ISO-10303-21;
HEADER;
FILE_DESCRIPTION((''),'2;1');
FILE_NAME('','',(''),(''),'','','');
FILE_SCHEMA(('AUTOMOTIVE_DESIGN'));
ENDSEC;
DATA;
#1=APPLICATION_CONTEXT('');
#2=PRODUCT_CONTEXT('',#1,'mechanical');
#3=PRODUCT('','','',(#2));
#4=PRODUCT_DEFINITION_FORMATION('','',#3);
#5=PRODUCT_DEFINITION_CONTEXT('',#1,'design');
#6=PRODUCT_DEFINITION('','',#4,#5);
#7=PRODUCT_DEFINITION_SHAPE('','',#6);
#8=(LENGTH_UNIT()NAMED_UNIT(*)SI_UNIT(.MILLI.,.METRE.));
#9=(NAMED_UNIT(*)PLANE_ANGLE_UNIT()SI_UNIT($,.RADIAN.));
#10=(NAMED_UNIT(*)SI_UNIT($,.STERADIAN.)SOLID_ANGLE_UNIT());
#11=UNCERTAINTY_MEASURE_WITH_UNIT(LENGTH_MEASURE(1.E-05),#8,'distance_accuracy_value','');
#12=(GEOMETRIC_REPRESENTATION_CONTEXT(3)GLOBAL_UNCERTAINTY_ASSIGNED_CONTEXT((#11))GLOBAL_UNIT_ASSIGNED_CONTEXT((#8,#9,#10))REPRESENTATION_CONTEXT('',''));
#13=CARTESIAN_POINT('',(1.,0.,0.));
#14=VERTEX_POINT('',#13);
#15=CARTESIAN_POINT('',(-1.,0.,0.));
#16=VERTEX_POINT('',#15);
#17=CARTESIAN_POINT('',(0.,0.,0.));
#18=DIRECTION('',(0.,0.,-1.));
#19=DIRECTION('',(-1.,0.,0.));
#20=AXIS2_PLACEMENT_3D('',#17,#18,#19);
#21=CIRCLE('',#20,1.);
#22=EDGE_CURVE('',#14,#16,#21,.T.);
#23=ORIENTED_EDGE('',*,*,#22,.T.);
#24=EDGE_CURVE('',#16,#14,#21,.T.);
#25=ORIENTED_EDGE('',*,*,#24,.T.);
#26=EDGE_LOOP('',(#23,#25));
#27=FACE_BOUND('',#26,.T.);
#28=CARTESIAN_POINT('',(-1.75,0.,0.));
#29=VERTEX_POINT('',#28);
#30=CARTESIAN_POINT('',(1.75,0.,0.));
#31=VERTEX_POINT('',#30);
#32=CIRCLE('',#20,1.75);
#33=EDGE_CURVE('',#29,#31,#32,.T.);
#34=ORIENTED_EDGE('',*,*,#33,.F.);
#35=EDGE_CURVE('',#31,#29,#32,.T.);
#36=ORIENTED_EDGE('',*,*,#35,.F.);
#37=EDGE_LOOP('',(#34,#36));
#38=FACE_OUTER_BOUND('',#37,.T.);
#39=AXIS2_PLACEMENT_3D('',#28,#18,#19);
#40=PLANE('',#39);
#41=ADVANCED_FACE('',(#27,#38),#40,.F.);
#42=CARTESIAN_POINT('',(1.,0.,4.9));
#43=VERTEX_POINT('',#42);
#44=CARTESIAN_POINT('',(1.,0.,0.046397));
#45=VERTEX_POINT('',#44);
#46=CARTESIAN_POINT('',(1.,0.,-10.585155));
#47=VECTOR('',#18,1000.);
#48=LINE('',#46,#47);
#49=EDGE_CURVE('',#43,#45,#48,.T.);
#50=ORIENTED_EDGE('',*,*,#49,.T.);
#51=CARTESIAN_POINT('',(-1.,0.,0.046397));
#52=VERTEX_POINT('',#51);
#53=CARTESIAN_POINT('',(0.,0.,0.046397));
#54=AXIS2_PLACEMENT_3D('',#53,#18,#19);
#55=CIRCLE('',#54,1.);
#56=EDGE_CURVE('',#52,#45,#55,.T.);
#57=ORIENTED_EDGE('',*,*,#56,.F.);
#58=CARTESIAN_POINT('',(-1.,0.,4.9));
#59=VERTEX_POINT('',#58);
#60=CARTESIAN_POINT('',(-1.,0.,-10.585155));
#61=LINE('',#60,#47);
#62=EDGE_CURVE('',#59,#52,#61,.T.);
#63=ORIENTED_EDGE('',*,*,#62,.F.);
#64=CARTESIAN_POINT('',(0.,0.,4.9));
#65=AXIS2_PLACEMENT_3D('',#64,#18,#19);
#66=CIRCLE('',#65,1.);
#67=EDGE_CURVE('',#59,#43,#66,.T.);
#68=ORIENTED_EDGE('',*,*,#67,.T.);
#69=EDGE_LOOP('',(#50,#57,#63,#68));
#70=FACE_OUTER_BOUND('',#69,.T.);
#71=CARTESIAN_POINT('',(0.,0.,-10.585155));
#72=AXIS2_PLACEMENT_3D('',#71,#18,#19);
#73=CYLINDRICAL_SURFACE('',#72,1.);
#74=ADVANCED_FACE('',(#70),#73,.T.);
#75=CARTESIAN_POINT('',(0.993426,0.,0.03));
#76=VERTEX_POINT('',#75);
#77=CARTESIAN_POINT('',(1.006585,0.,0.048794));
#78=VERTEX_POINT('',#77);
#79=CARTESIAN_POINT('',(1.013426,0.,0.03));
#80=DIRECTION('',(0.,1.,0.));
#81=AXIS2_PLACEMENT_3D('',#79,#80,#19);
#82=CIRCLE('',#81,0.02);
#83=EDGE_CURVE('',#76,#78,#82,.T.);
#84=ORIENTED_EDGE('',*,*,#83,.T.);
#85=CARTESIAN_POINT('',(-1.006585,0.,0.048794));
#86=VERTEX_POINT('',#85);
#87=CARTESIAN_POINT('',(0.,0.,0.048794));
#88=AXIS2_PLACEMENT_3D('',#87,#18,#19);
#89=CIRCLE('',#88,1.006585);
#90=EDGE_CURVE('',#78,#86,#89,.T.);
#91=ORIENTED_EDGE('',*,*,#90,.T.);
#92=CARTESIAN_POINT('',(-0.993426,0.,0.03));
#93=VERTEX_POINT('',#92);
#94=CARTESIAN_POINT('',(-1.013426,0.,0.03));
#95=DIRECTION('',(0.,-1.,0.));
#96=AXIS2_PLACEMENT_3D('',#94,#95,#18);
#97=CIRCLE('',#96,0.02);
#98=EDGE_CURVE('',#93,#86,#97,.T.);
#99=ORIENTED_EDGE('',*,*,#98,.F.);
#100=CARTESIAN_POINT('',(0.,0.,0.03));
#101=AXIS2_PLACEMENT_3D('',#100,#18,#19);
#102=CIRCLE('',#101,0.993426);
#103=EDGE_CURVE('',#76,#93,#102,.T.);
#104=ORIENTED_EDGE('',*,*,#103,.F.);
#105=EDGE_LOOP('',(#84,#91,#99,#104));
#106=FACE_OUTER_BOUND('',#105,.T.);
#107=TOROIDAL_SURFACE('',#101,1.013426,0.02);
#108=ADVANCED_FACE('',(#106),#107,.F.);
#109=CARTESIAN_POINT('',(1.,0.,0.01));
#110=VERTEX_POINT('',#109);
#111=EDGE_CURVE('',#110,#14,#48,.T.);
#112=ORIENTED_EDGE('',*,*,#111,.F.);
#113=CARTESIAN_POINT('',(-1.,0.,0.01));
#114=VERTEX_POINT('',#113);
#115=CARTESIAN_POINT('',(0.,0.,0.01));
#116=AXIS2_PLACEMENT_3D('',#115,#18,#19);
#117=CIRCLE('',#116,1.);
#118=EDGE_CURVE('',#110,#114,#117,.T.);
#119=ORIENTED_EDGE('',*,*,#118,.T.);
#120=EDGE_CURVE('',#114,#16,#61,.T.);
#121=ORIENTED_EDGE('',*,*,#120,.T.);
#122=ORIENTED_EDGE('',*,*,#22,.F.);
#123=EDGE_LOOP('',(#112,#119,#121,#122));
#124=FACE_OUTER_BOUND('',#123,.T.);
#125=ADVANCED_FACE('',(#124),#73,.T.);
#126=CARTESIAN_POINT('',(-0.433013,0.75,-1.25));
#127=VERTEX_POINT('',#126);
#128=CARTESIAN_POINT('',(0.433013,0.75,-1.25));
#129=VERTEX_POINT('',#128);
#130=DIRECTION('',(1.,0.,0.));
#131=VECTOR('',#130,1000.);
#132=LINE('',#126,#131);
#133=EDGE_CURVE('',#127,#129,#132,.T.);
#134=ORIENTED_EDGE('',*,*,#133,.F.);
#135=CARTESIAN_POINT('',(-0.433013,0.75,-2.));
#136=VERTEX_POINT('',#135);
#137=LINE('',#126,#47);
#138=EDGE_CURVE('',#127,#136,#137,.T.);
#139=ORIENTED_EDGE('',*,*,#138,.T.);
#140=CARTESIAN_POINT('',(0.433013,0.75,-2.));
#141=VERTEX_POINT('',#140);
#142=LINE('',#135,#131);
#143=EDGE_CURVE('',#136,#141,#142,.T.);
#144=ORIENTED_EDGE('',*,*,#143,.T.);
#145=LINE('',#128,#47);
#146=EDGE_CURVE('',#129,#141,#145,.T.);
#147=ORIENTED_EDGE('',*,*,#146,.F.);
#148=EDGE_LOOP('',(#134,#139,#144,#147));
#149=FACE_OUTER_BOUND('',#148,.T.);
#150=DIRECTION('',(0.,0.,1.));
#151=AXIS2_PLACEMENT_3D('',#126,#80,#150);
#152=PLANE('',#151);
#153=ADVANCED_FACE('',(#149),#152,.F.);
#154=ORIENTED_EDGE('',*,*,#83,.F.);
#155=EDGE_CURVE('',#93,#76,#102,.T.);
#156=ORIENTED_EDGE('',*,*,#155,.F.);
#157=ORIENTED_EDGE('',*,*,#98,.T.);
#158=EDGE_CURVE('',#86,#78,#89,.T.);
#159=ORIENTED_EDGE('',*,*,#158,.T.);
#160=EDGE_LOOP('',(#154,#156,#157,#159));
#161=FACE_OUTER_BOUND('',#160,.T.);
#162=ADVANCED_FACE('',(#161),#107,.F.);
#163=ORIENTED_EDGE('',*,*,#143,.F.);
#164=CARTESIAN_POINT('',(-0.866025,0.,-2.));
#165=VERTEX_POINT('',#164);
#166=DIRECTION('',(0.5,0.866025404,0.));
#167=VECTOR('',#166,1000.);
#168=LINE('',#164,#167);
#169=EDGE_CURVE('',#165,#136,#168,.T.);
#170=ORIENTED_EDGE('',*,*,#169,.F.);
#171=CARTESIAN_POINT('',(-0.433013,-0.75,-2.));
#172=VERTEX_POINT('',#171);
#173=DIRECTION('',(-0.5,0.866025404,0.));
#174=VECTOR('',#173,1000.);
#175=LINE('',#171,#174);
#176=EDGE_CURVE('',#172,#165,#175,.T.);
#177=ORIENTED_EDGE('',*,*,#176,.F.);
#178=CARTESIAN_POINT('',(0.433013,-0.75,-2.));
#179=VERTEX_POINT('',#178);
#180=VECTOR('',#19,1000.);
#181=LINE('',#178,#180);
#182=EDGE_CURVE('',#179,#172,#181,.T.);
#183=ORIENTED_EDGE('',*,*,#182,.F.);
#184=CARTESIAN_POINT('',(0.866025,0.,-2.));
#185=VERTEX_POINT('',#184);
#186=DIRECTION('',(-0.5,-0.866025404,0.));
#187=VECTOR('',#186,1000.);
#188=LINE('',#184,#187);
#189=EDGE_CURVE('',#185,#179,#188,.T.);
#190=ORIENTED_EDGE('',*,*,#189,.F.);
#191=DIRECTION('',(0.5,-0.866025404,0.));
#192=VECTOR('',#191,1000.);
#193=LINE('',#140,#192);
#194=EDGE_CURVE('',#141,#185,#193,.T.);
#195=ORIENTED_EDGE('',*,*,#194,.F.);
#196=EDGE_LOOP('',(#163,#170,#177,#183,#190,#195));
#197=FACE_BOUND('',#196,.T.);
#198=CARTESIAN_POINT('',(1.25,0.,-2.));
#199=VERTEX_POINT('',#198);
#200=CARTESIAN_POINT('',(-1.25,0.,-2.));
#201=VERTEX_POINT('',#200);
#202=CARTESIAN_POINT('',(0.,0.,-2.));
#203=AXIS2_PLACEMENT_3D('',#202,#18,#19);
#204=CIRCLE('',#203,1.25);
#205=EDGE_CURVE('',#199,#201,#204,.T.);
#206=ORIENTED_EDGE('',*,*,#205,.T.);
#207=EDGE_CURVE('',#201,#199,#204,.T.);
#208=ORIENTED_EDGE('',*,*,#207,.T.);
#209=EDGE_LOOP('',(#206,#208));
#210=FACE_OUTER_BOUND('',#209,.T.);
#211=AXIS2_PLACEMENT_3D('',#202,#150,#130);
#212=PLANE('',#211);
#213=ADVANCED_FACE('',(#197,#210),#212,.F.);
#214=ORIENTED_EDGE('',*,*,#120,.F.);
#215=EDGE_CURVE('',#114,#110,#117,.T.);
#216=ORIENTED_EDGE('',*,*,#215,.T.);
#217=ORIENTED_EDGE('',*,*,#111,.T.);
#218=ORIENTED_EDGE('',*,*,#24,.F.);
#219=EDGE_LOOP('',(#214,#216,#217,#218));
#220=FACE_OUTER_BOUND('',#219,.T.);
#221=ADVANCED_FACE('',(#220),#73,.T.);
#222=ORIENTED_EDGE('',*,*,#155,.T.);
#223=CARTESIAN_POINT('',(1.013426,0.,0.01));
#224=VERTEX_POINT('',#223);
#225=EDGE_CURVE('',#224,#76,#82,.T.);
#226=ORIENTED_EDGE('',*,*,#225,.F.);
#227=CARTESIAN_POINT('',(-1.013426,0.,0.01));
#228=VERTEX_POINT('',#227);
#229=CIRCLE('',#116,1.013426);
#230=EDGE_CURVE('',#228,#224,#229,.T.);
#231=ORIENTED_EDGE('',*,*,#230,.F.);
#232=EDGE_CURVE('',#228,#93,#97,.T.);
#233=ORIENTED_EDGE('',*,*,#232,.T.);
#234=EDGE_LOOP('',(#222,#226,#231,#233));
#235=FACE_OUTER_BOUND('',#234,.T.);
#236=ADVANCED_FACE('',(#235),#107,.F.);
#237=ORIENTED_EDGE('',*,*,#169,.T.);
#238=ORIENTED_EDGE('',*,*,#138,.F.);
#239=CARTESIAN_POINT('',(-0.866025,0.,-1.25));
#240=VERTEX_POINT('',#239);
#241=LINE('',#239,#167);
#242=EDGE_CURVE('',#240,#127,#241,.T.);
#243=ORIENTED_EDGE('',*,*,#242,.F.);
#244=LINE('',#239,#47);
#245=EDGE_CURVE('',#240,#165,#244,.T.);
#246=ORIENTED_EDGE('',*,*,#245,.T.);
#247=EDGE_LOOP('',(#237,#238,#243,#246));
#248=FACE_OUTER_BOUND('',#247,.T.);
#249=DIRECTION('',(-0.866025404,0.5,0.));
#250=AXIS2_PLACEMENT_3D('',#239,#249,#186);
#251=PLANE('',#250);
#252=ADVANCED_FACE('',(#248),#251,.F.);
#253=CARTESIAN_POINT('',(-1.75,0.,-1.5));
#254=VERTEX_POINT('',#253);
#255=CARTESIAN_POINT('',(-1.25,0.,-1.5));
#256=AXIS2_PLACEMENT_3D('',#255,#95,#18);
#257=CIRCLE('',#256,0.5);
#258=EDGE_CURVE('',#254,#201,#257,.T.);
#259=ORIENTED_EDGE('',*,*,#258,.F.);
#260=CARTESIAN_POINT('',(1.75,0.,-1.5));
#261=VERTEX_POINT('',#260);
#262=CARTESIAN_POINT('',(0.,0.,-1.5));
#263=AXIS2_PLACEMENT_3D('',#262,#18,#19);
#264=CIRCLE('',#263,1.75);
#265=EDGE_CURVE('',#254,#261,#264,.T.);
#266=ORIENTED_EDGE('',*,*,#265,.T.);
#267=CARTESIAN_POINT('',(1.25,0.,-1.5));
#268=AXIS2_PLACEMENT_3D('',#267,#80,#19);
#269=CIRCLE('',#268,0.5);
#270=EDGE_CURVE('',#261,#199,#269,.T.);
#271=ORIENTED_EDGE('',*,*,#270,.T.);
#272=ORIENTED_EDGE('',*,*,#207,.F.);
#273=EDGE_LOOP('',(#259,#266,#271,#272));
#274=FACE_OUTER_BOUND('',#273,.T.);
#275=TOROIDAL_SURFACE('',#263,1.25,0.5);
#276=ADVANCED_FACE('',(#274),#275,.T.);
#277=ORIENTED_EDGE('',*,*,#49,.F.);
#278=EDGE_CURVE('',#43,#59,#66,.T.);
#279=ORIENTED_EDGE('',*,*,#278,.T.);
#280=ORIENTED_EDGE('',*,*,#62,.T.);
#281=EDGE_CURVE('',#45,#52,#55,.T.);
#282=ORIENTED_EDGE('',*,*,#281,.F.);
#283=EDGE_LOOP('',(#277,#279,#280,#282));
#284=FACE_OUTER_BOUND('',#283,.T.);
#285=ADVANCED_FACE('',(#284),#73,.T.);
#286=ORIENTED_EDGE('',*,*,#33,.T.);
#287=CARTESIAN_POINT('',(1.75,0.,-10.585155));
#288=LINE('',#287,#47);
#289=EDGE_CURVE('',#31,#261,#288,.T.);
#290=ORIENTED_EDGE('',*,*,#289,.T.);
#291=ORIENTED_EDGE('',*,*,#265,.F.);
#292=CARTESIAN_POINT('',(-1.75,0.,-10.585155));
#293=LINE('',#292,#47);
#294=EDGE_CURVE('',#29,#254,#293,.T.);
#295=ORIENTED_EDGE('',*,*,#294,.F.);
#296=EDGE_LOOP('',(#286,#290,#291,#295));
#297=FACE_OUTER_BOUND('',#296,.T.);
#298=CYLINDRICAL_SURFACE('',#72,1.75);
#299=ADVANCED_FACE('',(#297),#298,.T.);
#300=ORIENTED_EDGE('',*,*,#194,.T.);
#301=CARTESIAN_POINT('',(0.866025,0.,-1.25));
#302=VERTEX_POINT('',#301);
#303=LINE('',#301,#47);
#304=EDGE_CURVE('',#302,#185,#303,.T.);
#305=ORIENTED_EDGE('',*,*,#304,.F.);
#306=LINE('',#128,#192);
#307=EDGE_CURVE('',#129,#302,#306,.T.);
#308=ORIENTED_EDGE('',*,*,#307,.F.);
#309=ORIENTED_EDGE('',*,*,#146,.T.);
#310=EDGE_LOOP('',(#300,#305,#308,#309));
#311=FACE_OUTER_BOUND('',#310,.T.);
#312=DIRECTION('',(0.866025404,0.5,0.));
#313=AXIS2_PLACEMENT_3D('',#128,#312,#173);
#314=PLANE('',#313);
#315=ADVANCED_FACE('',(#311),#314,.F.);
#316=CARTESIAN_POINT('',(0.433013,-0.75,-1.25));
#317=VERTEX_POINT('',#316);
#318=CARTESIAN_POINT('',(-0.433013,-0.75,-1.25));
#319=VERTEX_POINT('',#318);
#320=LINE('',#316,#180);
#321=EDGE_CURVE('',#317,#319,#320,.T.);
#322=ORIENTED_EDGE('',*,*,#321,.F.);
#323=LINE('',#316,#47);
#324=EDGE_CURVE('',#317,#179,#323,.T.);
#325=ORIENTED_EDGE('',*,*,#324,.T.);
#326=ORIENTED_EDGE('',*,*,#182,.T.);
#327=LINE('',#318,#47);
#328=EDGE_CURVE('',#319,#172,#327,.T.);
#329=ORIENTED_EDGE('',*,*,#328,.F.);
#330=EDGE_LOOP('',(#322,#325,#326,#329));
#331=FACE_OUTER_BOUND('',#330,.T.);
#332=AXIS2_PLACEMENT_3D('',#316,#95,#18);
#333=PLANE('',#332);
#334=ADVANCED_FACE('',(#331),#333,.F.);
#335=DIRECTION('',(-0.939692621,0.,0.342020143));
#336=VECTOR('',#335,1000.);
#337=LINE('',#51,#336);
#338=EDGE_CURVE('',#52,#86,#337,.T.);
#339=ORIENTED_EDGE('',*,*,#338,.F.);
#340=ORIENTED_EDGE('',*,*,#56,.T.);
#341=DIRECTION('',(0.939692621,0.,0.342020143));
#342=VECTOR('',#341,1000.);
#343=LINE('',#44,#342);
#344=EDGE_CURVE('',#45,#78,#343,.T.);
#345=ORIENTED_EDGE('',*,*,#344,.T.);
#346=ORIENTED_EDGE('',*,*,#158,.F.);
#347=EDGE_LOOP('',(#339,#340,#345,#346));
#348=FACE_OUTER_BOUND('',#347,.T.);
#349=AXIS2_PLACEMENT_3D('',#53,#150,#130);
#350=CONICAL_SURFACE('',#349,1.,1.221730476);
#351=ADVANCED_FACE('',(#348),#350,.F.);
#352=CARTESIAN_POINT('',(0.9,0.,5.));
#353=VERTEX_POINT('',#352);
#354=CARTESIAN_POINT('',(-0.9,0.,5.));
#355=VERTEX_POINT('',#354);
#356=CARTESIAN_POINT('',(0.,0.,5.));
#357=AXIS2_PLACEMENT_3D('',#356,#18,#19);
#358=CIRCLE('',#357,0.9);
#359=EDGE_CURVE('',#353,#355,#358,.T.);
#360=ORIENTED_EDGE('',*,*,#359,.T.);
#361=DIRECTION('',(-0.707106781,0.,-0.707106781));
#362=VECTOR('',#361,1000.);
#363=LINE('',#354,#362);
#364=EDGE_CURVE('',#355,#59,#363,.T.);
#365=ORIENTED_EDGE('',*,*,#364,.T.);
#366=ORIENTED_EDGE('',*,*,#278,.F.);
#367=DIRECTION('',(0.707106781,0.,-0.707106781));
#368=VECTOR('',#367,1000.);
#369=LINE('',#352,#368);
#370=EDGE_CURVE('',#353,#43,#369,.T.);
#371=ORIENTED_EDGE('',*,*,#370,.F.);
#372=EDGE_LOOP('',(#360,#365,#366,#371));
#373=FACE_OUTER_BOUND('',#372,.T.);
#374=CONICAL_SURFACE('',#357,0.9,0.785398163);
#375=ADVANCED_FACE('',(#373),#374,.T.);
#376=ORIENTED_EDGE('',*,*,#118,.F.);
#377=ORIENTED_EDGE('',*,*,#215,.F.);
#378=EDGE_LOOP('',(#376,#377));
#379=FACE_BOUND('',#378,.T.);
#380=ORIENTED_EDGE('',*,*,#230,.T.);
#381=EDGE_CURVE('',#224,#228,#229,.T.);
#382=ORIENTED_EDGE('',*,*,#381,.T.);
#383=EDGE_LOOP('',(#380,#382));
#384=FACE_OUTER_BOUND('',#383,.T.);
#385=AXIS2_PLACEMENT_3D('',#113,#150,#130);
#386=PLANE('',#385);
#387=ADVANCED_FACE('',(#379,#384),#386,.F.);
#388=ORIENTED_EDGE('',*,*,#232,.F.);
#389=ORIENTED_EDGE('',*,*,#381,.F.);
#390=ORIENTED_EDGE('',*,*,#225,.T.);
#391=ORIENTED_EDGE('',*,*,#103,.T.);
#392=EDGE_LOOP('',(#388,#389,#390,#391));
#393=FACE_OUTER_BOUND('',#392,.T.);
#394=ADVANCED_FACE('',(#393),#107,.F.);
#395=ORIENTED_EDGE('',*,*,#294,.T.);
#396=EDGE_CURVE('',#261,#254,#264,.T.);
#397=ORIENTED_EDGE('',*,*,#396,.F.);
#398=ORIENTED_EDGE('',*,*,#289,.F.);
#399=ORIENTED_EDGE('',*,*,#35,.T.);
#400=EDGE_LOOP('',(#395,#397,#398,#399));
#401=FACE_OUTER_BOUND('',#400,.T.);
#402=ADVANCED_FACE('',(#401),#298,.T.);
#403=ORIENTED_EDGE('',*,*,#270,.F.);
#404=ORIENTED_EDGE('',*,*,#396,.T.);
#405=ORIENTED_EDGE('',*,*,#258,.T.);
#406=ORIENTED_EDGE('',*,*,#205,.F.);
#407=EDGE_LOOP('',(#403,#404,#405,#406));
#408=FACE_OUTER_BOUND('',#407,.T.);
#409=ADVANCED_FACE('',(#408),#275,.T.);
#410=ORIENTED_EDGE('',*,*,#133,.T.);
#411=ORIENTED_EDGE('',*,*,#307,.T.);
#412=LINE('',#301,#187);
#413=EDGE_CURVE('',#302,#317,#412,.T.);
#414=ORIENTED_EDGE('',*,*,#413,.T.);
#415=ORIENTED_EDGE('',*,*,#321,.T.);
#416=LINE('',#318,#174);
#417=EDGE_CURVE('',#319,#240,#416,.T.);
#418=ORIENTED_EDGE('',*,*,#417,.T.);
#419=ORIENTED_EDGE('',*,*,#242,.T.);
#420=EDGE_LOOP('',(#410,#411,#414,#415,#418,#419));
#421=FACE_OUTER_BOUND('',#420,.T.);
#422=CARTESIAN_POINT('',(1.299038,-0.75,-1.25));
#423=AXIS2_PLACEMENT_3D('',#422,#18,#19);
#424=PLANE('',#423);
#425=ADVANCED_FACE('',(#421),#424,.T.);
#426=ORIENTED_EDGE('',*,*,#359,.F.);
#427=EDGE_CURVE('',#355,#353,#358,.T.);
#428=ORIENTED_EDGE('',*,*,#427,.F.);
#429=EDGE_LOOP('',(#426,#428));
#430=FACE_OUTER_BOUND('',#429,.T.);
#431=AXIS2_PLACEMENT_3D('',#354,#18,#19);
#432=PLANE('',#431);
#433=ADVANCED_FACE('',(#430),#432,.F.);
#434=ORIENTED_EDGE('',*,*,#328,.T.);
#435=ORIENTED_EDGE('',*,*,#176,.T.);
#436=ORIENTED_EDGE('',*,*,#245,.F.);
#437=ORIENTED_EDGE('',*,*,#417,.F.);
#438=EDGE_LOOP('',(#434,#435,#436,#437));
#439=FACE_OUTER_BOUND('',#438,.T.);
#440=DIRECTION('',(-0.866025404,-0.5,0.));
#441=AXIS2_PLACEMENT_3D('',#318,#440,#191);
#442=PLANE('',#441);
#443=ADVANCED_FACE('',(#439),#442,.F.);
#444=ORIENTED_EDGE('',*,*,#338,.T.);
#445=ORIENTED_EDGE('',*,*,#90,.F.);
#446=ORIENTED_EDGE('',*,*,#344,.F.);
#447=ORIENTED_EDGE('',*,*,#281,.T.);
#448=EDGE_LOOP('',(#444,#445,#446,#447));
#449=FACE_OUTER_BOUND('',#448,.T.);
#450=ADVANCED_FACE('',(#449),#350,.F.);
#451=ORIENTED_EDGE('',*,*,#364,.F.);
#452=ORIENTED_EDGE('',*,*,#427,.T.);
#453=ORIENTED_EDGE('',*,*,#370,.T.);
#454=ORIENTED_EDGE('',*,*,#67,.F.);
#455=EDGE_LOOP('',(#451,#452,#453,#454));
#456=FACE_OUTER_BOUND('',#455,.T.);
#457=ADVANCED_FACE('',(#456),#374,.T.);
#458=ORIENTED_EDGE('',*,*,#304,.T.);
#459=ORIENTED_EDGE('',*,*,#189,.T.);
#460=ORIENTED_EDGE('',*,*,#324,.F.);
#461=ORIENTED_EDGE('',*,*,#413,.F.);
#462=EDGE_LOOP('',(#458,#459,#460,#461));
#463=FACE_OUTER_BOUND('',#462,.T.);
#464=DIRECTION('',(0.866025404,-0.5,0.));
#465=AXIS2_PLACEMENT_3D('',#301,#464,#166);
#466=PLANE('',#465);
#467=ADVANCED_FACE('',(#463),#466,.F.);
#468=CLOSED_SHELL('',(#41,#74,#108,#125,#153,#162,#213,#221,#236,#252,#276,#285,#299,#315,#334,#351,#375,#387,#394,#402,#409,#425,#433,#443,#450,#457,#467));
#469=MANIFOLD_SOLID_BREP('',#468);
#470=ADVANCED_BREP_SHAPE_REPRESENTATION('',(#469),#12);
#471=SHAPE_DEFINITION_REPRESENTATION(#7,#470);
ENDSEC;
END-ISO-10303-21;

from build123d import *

# Parameters (mm, degrees)
CUT_EXTRUDE1_DEPTH = 0.75


with BuildPart() as part:
    # Logo3_bib1 → Revolve1 (revolve)
    with BuildSketch(Plane(origin=(0, 0, 0), x_dir=(-1, 0, 0), z_dir=(0, -1, 0))):
        with BuildLine():
            Line((0, -5), (0, 2))
            Line((0, 2), (1.25, 2))
            ThreePointArc((1.25, 2), (1.603553391, 1.853553391), (1.75, 1.5))
            Line((1.75, 1.5), (1.75, 0))
            Line((1.75, 0), (1, 0))
            Line((1, 0), (1, -0.01))
            Line((1, -0.01), (1.013425636, -0.01))
            ThreePointArc((1.013425636, -0.01), (0.993729481, -0.026527036), (1.006585234, -0.048793852))
            Line((1.006585234, -0.048793852), (1, -0.046397023))
            Line((1, -0.046397023), (1, -4.9))
            Line((1, -4.9), (0.9, -5))
            Line((0.9, -5), (0, -5))
        make_face()
    revolve(axis=Axis((0, 0, -10.585154653), (0, 0, 1)))

    # Logo3_bib2 → Cut-Extrude1 (cut)
    with BuildSketch(Plane(origin=(0, 0, -2), x_dir=(1, 0, 0), z_dir=(0, 0, -1))):
        Polygon((0.866025404, 0), (0.433012702, 0.75), (-0.433012702, 0.75), (-0.866025404, 0), (-0.433012702, -0.75), (0.433012702, -0.75), align=None)
    extrude(amount=-CUT_EXTRUDE1_DEPTH, mode=Mode.SUBTRACT)


solid = part.part
